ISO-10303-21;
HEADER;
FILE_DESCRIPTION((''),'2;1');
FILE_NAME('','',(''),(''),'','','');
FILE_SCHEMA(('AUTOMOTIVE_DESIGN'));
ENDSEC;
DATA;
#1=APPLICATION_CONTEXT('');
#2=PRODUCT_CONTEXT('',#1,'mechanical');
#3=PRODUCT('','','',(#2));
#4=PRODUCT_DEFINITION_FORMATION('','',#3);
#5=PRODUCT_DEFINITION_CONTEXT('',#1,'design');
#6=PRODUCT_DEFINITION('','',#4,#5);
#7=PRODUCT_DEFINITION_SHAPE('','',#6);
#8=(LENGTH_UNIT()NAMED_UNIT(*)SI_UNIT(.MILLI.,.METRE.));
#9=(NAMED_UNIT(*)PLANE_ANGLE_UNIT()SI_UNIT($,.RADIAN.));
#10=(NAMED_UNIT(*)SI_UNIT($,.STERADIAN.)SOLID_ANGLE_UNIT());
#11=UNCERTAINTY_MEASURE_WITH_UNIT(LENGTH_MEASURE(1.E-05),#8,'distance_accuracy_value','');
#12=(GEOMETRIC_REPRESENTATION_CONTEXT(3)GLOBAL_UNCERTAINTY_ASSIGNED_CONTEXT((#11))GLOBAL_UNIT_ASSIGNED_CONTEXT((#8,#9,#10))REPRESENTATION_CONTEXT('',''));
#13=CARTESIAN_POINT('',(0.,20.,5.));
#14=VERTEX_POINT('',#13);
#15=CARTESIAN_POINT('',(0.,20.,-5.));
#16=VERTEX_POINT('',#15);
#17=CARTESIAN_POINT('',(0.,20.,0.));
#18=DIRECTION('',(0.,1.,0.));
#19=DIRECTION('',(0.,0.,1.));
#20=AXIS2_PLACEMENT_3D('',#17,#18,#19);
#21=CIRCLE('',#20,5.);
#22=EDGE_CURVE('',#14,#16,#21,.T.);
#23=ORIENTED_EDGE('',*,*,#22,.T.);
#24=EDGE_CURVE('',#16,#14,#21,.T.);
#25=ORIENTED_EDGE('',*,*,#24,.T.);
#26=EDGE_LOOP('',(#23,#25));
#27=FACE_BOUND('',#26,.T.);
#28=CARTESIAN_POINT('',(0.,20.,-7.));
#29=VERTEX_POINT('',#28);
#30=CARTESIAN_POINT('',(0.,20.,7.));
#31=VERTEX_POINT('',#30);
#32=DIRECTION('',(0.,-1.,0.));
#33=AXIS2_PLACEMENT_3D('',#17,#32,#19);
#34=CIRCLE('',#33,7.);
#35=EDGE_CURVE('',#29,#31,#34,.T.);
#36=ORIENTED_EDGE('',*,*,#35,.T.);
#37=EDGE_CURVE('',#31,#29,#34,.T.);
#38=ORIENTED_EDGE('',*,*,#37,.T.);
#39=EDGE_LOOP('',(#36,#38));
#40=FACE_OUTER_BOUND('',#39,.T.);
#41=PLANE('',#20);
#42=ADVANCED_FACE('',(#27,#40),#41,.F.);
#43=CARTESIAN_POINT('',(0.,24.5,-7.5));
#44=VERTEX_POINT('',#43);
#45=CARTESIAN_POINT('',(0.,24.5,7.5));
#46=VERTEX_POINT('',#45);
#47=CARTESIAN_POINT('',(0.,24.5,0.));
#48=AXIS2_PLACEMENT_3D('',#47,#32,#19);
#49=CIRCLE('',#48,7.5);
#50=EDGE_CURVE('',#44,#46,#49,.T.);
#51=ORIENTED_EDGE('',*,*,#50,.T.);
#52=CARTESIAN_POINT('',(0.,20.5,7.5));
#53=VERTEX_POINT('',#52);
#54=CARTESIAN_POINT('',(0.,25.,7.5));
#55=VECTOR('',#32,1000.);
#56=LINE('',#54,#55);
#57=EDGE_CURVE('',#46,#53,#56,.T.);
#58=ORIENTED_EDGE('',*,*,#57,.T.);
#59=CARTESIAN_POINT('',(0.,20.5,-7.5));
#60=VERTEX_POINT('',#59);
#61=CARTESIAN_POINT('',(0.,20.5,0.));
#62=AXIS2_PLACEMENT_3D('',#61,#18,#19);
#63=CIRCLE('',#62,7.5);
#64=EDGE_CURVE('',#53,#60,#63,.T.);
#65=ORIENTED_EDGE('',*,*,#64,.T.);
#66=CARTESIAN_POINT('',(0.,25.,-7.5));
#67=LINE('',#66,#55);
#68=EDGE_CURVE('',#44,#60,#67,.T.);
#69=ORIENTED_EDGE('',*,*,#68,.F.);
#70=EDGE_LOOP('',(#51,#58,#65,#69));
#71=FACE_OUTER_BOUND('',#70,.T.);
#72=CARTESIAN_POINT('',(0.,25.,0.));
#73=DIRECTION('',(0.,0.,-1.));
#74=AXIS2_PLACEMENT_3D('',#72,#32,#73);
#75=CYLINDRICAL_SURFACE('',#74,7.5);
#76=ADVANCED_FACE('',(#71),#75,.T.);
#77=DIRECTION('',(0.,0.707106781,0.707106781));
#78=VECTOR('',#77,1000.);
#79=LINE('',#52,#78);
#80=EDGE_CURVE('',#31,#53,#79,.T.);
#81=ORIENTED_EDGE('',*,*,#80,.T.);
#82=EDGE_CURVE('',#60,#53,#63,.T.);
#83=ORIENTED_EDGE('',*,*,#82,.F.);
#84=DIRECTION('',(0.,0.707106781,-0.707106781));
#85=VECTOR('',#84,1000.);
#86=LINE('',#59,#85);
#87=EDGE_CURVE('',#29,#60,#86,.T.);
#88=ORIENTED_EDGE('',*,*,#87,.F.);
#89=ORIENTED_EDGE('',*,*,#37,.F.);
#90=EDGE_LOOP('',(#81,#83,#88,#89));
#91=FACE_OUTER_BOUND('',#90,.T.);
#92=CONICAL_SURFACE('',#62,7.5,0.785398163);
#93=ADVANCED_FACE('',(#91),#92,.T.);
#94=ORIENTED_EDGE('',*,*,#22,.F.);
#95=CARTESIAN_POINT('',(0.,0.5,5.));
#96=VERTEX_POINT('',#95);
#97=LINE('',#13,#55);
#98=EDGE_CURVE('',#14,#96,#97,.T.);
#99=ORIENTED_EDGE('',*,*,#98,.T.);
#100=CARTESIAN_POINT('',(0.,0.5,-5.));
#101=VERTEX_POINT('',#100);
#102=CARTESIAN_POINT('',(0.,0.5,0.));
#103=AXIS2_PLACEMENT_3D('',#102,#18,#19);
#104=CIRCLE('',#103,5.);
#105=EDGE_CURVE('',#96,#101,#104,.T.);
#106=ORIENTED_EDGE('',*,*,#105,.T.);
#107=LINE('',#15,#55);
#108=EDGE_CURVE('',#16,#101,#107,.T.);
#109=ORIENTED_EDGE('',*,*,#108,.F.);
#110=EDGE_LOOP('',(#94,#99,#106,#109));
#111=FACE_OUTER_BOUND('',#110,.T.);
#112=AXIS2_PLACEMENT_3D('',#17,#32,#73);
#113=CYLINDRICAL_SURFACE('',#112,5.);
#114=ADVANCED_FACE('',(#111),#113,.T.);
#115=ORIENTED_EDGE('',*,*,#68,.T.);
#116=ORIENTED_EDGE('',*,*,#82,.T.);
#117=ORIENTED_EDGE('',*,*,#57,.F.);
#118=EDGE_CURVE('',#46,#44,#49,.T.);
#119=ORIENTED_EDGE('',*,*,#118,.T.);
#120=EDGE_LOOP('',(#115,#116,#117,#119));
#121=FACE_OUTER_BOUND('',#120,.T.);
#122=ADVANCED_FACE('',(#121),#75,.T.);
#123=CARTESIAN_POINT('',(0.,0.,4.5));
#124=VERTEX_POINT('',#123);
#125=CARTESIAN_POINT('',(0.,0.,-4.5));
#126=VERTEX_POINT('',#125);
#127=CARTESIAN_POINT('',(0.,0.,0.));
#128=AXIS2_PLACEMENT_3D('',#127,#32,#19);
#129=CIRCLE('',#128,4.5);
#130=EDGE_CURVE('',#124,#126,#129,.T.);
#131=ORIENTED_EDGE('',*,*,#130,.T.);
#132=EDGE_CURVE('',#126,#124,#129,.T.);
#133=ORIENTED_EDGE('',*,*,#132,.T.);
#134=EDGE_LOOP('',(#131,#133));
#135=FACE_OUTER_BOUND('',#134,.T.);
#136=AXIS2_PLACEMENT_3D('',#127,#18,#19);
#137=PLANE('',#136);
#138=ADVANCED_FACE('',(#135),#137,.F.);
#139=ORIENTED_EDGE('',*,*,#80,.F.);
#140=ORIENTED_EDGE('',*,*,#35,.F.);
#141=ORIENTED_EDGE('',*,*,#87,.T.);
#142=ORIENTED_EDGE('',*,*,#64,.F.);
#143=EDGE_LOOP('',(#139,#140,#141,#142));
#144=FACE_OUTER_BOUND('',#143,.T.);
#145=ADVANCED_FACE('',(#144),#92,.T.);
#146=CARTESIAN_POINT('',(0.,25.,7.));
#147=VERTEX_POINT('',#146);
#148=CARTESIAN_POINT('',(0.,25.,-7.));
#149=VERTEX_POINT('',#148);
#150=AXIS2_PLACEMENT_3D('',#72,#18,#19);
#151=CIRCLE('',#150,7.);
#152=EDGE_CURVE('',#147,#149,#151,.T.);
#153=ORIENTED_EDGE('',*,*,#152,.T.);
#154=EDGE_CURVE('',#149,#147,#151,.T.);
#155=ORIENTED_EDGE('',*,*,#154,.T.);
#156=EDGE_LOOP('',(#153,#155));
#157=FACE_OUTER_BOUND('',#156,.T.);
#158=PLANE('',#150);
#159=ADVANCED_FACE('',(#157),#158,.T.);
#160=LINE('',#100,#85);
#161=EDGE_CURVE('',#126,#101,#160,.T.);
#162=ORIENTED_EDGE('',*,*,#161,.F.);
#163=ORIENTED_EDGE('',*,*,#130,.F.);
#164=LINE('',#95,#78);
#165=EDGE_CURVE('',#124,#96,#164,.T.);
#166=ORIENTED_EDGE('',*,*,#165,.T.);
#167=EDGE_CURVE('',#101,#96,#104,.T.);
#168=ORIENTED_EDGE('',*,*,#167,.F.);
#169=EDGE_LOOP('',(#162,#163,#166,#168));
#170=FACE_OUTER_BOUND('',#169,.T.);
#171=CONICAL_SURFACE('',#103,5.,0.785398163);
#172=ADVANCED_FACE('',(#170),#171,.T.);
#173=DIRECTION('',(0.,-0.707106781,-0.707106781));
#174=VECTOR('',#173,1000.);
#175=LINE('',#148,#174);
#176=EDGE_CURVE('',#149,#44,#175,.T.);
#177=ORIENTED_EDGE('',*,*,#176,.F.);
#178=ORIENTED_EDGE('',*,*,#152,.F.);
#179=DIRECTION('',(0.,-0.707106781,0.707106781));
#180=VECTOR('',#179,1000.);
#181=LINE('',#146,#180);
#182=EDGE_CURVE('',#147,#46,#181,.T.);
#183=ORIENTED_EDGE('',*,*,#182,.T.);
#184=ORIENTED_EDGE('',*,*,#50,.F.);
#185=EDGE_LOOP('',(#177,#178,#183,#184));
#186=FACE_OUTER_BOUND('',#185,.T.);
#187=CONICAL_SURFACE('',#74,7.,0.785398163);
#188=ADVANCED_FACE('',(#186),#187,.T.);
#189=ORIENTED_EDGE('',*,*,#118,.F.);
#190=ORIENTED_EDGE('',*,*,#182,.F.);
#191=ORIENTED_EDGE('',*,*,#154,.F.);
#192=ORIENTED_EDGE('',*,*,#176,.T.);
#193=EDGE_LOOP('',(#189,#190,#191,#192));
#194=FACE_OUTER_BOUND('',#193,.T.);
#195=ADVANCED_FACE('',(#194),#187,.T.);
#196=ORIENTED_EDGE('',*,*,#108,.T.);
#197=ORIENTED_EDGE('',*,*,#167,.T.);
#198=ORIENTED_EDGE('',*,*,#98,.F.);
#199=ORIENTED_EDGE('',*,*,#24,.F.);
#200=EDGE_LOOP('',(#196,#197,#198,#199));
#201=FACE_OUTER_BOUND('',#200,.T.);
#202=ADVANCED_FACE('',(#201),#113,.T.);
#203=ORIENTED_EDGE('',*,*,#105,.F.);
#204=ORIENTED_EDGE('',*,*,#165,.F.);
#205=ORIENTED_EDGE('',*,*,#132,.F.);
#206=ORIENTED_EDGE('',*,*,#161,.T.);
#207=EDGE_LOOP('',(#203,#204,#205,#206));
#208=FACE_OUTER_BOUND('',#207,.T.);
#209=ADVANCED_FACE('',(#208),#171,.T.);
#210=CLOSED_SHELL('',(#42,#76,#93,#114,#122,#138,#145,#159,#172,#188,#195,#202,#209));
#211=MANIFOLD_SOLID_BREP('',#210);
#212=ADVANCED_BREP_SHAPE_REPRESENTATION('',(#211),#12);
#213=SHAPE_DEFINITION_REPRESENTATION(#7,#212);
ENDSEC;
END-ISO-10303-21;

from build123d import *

# Parameters (mm, degrees)
SKETCH2_R           = 5
BOSS_EXTRUDE1_DEPTH = 20
SKETCH3_R           = 7.5
BOSS_EXTRUDE2_DEPTH = 5
CHAMFER2_SIZE       = 0.5


with BuildPart() as part:
    # Sketch2 → Boss-Extrude1 (new body)
    with BuildSketch(Plane(origin=(0, 0, 0), x_dir=(1, 0, 0), z_dir=(0, 1, 0))):
        with Locations(Location((0, 0, 0), (0, 0, 270))):
            Circle(SKETCH2_R)
    extrude(amount=BOSS_EXTRUDE1_DEPTH)

    # Sketch3 → Boss-Extrude2 (add)
    with BuildSketch(Plane(origin=(0, 20, 0), x_dir=(1, 0, 0), z_dir=(0, 1, 0))):
        with Locations(Location((0, 0, 0), (0, 0, 270))):
            Circle(SKETCH3_R)
    extrude(amount=BOSS_EXTRUDE2_DEPTH)

    # Chamfer2
    chamfer2_edges = [part.edges().sort_by_distance(p)[0] for p in [
        (0, 0, -5),
        (0, 20, -7.5),
        (0, 25, -7.5),
    ]]
    chamfer(chamfer2_edges, length=CHAMFER2_SIZE)


solid = part.part
